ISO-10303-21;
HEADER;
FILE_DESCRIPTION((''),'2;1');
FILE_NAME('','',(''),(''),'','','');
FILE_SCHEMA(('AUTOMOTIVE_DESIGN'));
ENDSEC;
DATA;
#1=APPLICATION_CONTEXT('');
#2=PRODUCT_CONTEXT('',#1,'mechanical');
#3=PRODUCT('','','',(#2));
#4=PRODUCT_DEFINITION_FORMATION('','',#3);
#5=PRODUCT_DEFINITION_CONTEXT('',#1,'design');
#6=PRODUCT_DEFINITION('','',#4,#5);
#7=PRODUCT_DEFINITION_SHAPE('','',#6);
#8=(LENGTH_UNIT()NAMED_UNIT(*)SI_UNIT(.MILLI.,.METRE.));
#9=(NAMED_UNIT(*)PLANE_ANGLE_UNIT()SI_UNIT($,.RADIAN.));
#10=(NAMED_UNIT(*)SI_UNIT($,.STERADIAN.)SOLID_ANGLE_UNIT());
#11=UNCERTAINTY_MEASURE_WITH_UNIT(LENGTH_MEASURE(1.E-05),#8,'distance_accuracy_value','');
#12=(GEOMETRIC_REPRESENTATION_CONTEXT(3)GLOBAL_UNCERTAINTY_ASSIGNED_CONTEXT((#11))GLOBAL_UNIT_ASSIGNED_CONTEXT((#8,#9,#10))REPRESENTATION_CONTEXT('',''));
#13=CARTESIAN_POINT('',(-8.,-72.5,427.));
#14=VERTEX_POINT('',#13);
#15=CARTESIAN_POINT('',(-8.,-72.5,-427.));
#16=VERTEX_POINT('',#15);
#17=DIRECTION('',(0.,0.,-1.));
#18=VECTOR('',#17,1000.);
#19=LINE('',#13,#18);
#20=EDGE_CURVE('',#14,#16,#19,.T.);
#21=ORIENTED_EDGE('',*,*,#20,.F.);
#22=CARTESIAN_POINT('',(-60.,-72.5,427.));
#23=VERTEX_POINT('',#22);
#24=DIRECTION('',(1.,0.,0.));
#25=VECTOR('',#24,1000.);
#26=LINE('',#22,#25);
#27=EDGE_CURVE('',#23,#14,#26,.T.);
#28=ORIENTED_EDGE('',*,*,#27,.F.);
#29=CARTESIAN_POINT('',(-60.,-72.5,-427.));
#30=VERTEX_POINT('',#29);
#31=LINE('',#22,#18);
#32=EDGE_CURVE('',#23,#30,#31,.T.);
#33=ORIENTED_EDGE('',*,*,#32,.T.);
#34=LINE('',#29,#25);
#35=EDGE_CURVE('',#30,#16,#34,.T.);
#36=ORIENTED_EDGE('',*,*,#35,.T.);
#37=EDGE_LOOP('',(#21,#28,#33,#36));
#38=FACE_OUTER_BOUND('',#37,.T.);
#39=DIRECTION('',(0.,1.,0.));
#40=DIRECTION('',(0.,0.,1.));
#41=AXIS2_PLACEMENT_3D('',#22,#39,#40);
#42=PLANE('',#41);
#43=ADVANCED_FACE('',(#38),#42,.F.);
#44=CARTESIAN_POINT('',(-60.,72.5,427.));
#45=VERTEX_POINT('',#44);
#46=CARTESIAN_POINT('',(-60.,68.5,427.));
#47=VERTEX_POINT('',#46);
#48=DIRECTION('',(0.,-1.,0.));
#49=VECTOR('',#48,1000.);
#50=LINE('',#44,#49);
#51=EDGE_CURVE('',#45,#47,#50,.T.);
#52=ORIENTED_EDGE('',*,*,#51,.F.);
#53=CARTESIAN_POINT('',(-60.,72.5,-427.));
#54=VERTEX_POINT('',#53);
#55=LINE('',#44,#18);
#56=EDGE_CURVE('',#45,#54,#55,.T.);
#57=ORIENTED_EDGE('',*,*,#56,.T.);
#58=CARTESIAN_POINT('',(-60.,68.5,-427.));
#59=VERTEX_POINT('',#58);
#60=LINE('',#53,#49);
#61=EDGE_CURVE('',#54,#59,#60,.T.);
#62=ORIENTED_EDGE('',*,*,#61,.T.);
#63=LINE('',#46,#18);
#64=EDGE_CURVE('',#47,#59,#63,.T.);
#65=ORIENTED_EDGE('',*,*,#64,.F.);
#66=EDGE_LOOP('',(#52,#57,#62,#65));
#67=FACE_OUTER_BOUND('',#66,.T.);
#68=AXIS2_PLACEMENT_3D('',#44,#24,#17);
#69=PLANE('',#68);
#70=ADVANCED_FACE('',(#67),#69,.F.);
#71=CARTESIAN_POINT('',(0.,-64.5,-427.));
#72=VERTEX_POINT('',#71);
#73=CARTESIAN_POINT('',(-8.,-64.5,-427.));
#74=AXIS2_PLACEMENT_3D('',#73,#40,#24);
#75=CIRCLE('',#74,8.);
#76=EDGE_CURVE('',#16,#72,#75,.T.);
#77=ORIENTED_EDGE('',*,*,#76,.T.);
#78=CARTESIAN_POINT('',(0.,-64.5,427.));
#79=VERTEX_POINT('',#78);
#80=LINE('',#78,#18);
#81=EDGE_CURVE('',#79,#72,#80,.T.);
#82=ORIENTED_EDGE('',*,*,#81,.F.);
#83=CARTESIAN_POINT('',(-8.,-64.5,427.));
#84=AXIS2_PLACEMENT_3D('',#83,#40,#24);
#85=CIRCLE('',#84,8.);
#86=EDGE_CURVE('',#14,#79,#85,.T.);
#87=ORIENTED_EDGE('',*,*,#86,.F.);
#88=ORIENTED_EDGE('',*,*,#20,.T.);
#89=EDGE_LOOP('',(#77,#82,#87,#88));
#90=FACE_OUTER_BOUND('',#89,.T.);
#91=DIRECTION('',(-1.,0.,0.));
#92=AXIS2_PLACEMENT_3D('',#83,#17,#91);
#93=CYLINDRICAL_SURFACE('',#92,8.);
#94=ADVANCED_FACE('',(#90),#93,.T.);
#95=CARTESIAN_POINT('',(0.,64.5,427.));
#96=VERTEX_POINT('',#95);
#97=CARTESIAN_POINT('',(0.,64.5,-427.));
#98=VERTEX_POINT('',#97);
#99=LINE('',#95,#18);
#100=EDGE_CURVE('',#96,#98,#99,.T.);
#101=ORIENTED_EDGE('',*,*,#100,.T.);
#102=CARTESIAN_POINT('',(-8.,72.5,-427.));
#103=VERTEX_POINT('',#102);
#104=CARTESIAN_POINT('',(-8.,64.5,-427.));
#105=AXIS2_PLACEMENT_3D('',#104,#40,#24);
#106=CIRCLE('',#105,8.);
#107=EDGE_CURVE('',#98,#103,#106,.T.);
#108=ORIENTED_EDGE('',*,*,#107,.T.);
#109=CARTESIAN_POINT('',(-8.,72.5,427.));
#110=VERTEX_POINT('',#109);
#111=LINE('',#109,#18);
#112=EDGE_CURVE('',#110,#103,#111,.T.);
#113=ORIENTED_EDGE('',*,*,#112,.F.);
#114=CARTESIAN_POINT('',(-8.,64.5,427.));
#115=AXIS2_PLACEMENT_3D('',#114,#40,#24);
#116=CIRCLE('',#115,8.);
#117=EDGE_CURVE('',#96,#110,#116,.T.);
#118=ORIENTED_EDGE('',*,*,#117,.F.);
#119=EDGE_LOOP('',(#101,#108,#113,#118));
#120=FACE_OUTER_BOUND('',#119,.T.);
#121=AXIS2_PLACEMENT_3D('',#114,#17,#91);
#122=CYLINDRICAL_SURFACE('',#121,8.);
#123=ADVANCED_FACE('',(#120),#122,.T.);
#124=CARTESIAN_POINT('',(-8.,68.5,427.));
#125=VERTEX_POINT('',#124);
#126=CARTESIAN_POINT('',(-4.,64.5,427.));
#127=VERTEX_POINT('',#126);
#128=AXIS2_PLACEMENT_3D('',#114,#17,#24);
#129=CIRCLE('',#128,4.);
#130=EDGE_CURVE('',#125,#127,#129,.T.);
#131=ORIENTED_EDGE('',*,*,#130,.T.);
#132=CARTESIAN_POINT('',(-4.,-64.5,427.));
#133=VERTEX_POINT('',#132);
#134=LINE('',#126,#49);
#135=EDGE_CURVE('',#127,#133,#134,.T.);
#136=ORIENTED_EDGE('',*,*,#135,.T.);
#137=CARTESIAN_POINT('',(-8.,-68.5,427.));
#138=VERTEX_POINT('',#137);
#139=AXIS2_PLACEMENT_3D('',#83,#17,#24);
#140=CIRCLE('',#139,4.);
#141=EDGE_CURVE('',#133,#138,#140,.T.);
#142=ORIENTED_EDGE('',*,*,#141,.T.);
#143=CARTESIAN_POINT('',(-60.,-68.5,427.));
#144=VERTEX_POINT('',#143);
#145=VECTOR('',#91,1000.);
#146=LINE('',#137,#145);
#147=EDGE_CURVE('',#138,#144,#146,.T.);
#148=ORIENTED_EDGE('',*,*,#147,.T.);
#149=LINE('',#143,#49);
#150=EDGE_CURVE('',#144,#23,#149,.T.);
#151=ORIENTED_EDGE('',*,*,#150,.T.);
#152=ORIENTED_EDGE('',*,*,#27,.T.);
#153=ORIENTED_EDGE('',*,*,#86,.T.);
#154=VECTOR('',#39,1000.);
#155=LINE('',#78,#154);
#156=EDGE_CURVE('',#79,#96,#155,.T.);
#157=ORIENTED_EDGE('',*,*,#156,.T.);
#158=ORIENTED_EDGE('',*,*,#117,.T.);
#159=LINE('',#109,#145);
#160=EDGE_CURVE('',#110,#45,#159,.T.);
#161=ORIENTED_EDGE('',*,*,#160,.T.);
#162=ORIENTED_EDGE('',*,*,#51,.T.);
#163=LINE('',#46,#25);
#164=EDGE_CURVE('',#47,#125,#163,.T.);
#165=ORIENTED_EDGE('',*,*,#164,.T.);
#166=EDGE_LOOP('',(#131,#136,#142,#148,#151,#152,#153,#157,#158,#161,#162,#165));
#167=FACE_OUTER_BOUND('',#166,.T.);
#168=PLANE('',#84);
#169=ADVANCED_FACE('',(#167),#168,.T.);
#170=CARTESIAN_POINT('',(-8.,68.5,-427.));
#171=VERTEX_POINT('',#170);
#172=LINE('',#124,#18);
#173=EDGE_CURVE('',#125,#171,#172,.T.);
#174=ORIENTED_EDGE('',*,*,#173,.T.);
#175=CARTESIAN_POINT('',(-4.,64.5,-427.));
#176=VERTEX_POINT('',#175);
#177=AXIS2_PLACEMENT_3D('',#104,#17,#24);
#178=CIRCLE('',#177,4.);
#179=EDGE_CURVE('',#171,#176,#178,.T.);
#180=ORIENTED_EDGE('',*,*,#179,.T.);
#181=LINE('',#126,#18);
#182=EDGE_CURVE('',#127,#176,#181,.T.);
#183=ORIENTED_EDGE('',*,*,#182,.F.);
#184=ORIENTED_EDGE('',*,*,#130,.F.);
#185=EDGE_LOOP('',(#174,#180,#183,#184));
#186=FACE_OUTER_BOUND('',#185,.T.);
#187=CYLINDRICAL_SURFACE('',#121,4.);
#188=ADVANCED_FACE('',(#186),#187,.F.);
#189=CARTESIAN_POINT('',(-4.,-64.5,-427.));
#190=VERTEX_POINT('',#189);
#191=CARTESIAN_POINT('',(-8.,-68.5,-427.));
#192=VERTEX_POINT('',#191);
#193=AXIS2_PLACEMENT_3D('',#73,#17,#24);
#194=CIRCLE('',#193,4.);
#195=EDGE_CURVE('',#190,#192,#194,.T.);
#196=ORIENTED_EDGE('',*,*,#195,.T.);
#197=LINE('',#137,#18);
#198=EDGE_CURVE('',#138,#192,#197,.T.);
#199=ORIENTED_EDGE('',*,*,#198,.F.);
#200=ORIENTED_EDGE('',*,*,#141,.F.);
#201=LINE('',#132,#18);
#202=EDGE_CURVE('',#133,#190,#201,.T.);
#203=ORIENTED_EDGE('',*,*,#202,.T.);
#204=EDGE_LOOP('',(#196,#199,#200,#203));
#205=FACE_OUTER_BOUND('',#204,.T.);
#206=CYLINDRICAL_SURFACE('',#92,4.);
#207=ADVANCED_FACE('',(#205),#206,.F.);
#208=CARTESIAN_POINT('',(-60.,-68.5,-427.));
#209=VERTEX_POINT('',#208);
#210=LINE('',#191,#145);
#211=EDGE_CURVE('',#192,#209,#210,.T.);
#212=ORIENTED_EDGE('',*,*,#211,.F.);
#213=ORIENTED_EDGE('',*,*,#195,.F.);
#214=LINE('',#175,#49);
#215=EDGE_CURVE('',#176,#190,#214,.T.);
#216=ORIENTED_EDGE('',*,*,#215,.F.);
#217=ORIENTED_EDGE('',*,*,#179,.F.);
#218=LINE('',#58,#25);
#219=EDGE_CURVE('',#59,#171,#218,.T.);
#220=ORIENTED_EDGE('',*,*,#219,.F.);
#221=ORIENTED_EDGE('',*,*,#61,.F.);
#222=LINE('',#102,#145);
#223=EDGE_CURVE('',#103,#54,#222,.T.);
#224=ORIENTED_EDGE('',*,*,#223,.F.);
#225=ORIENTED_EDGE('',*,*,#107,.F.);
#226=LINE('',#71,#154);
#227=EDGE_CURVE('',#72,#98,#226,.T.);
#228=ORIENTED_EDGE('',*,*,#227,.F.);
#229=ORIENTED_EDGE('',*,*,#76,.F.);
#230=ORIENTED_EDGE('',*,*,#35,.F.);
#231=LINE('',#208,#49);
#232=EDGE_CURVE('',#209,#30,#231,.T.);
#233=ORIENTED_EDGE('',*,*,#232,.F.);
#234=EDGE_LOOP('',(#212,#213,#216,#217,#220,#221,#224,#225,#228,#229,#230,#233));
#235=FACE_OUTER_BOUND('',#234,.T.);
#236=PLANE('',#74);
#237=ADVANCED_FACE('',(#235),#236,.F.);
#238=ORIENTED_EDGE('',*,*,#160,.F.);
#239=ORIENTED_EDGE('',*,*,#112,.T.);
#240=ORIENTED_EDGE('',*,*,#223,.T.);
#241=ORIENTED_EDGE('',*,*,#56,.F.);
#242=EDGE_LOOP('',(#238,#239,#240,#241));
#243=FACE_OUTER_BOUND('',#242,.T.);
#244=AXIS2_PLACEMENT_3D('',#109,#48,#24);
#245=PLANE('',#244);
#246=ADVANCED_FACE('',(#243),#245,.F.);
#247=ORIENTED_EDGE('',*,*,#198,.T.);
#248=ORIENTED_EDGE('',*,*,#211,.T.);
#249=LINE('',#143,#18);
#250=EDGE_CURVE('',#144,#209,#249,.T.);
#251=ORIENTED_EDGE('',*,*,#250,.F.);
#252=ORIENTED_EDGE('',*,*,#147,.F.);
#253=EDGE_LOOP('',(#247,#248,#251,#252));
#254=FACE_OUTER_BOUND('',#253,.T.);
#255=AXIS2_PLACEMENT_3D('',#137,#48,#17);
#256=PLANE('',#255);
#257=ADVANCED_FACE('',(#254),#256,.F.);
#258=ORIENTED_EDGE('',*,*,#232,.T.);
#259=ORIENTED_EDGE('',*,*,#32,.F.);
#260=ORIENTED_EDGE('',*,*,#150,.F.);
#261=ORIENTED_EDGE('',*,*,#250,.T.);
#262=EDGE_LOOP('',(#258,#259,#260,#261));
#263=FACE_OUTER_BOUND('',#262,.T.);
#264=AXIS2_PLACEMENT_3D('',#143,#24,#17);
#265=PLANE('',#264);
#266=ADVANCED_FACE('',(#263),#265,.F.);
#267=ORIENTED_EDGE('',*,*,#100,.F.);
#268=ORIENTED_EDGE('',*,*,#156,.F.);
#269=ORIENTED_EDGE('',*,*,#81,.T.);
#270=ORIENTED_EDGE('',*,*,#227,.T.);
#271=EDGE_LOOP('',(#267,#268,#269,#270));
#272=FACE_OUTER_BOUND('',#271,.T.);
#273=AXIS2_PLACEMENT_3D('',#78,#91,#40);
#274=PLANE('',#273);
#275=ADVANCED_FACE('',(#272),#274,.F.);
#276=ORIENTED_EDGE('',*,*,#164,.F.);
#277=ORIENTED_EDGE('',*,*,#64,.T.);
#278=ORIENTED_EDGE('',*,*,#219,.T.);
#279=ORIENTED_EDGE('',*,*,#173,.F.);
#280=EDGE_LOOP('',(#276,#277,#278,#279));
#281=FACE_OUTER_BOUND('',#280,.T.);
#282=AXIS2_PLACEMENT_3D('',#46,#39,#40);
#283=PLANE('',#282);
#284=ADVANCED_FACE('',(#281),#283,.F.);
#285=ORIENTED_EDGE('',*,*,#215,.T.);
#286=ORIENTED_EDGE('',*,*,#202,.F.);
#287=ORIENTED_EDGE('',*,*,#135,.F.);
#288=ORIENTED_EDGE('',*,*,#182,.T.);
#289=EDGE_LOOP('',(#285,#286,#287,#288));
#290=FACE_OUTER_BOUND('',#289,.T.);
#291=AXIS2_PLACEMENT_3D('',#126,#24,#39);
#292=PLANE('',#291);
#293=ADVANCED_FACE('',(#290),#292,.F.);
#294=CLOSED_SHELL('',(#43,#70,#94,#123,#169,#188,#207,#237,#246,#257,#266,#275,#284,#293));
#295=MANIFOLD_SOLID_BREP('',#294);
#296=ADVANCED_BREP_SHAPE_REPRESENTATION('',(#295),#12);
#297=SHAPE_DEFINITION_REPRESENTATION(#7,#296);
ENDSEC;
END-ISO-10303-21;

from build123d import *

# Parameters (mm, degrees)
BOSS_EXTRUDE1_DEPTH = 427


with BuildPart() as part:
    # Sketch1 → Boss-Extrude1 (new, symmetric)
    with BuildSketch(Plane.XY):
        with BuildLine():
            Line((-60, -72.5), (-8, -72.5))
            ThreePointArc((-8, -72.5), (-2.343145751, -70.156854249), (0, -64.5))
            Line((0, -64.5), (0, 64.5))
            ThreePointArc((0, 64.5), (-2.343145751, 70.156854249), (-8, 72.5))
            Line((-8, 72.5), (-60, 72.5))
            Line((-60, 72.5), (-60, 68.5))
            Line((-60, 68.5), (-8, 68.5))
            ThreePointArc((-8, 68.5), (-5.171572875, 67.328427125), (-4, 64.5))
            Line((-4, 64.5), (-4, -64.5))
            ThreePointArc((-4, -64.5), (-5.171572875, -67.328427125), (-8, -68.5))
            Line((-8, -68.5), (-60, -68.5))
            Line((-60, -68.5), (-60, -72.5))
        make_face()
    extrude(amount=BOSS_EXTRUDE1_DEPTH, both=True)


solid = part.part
